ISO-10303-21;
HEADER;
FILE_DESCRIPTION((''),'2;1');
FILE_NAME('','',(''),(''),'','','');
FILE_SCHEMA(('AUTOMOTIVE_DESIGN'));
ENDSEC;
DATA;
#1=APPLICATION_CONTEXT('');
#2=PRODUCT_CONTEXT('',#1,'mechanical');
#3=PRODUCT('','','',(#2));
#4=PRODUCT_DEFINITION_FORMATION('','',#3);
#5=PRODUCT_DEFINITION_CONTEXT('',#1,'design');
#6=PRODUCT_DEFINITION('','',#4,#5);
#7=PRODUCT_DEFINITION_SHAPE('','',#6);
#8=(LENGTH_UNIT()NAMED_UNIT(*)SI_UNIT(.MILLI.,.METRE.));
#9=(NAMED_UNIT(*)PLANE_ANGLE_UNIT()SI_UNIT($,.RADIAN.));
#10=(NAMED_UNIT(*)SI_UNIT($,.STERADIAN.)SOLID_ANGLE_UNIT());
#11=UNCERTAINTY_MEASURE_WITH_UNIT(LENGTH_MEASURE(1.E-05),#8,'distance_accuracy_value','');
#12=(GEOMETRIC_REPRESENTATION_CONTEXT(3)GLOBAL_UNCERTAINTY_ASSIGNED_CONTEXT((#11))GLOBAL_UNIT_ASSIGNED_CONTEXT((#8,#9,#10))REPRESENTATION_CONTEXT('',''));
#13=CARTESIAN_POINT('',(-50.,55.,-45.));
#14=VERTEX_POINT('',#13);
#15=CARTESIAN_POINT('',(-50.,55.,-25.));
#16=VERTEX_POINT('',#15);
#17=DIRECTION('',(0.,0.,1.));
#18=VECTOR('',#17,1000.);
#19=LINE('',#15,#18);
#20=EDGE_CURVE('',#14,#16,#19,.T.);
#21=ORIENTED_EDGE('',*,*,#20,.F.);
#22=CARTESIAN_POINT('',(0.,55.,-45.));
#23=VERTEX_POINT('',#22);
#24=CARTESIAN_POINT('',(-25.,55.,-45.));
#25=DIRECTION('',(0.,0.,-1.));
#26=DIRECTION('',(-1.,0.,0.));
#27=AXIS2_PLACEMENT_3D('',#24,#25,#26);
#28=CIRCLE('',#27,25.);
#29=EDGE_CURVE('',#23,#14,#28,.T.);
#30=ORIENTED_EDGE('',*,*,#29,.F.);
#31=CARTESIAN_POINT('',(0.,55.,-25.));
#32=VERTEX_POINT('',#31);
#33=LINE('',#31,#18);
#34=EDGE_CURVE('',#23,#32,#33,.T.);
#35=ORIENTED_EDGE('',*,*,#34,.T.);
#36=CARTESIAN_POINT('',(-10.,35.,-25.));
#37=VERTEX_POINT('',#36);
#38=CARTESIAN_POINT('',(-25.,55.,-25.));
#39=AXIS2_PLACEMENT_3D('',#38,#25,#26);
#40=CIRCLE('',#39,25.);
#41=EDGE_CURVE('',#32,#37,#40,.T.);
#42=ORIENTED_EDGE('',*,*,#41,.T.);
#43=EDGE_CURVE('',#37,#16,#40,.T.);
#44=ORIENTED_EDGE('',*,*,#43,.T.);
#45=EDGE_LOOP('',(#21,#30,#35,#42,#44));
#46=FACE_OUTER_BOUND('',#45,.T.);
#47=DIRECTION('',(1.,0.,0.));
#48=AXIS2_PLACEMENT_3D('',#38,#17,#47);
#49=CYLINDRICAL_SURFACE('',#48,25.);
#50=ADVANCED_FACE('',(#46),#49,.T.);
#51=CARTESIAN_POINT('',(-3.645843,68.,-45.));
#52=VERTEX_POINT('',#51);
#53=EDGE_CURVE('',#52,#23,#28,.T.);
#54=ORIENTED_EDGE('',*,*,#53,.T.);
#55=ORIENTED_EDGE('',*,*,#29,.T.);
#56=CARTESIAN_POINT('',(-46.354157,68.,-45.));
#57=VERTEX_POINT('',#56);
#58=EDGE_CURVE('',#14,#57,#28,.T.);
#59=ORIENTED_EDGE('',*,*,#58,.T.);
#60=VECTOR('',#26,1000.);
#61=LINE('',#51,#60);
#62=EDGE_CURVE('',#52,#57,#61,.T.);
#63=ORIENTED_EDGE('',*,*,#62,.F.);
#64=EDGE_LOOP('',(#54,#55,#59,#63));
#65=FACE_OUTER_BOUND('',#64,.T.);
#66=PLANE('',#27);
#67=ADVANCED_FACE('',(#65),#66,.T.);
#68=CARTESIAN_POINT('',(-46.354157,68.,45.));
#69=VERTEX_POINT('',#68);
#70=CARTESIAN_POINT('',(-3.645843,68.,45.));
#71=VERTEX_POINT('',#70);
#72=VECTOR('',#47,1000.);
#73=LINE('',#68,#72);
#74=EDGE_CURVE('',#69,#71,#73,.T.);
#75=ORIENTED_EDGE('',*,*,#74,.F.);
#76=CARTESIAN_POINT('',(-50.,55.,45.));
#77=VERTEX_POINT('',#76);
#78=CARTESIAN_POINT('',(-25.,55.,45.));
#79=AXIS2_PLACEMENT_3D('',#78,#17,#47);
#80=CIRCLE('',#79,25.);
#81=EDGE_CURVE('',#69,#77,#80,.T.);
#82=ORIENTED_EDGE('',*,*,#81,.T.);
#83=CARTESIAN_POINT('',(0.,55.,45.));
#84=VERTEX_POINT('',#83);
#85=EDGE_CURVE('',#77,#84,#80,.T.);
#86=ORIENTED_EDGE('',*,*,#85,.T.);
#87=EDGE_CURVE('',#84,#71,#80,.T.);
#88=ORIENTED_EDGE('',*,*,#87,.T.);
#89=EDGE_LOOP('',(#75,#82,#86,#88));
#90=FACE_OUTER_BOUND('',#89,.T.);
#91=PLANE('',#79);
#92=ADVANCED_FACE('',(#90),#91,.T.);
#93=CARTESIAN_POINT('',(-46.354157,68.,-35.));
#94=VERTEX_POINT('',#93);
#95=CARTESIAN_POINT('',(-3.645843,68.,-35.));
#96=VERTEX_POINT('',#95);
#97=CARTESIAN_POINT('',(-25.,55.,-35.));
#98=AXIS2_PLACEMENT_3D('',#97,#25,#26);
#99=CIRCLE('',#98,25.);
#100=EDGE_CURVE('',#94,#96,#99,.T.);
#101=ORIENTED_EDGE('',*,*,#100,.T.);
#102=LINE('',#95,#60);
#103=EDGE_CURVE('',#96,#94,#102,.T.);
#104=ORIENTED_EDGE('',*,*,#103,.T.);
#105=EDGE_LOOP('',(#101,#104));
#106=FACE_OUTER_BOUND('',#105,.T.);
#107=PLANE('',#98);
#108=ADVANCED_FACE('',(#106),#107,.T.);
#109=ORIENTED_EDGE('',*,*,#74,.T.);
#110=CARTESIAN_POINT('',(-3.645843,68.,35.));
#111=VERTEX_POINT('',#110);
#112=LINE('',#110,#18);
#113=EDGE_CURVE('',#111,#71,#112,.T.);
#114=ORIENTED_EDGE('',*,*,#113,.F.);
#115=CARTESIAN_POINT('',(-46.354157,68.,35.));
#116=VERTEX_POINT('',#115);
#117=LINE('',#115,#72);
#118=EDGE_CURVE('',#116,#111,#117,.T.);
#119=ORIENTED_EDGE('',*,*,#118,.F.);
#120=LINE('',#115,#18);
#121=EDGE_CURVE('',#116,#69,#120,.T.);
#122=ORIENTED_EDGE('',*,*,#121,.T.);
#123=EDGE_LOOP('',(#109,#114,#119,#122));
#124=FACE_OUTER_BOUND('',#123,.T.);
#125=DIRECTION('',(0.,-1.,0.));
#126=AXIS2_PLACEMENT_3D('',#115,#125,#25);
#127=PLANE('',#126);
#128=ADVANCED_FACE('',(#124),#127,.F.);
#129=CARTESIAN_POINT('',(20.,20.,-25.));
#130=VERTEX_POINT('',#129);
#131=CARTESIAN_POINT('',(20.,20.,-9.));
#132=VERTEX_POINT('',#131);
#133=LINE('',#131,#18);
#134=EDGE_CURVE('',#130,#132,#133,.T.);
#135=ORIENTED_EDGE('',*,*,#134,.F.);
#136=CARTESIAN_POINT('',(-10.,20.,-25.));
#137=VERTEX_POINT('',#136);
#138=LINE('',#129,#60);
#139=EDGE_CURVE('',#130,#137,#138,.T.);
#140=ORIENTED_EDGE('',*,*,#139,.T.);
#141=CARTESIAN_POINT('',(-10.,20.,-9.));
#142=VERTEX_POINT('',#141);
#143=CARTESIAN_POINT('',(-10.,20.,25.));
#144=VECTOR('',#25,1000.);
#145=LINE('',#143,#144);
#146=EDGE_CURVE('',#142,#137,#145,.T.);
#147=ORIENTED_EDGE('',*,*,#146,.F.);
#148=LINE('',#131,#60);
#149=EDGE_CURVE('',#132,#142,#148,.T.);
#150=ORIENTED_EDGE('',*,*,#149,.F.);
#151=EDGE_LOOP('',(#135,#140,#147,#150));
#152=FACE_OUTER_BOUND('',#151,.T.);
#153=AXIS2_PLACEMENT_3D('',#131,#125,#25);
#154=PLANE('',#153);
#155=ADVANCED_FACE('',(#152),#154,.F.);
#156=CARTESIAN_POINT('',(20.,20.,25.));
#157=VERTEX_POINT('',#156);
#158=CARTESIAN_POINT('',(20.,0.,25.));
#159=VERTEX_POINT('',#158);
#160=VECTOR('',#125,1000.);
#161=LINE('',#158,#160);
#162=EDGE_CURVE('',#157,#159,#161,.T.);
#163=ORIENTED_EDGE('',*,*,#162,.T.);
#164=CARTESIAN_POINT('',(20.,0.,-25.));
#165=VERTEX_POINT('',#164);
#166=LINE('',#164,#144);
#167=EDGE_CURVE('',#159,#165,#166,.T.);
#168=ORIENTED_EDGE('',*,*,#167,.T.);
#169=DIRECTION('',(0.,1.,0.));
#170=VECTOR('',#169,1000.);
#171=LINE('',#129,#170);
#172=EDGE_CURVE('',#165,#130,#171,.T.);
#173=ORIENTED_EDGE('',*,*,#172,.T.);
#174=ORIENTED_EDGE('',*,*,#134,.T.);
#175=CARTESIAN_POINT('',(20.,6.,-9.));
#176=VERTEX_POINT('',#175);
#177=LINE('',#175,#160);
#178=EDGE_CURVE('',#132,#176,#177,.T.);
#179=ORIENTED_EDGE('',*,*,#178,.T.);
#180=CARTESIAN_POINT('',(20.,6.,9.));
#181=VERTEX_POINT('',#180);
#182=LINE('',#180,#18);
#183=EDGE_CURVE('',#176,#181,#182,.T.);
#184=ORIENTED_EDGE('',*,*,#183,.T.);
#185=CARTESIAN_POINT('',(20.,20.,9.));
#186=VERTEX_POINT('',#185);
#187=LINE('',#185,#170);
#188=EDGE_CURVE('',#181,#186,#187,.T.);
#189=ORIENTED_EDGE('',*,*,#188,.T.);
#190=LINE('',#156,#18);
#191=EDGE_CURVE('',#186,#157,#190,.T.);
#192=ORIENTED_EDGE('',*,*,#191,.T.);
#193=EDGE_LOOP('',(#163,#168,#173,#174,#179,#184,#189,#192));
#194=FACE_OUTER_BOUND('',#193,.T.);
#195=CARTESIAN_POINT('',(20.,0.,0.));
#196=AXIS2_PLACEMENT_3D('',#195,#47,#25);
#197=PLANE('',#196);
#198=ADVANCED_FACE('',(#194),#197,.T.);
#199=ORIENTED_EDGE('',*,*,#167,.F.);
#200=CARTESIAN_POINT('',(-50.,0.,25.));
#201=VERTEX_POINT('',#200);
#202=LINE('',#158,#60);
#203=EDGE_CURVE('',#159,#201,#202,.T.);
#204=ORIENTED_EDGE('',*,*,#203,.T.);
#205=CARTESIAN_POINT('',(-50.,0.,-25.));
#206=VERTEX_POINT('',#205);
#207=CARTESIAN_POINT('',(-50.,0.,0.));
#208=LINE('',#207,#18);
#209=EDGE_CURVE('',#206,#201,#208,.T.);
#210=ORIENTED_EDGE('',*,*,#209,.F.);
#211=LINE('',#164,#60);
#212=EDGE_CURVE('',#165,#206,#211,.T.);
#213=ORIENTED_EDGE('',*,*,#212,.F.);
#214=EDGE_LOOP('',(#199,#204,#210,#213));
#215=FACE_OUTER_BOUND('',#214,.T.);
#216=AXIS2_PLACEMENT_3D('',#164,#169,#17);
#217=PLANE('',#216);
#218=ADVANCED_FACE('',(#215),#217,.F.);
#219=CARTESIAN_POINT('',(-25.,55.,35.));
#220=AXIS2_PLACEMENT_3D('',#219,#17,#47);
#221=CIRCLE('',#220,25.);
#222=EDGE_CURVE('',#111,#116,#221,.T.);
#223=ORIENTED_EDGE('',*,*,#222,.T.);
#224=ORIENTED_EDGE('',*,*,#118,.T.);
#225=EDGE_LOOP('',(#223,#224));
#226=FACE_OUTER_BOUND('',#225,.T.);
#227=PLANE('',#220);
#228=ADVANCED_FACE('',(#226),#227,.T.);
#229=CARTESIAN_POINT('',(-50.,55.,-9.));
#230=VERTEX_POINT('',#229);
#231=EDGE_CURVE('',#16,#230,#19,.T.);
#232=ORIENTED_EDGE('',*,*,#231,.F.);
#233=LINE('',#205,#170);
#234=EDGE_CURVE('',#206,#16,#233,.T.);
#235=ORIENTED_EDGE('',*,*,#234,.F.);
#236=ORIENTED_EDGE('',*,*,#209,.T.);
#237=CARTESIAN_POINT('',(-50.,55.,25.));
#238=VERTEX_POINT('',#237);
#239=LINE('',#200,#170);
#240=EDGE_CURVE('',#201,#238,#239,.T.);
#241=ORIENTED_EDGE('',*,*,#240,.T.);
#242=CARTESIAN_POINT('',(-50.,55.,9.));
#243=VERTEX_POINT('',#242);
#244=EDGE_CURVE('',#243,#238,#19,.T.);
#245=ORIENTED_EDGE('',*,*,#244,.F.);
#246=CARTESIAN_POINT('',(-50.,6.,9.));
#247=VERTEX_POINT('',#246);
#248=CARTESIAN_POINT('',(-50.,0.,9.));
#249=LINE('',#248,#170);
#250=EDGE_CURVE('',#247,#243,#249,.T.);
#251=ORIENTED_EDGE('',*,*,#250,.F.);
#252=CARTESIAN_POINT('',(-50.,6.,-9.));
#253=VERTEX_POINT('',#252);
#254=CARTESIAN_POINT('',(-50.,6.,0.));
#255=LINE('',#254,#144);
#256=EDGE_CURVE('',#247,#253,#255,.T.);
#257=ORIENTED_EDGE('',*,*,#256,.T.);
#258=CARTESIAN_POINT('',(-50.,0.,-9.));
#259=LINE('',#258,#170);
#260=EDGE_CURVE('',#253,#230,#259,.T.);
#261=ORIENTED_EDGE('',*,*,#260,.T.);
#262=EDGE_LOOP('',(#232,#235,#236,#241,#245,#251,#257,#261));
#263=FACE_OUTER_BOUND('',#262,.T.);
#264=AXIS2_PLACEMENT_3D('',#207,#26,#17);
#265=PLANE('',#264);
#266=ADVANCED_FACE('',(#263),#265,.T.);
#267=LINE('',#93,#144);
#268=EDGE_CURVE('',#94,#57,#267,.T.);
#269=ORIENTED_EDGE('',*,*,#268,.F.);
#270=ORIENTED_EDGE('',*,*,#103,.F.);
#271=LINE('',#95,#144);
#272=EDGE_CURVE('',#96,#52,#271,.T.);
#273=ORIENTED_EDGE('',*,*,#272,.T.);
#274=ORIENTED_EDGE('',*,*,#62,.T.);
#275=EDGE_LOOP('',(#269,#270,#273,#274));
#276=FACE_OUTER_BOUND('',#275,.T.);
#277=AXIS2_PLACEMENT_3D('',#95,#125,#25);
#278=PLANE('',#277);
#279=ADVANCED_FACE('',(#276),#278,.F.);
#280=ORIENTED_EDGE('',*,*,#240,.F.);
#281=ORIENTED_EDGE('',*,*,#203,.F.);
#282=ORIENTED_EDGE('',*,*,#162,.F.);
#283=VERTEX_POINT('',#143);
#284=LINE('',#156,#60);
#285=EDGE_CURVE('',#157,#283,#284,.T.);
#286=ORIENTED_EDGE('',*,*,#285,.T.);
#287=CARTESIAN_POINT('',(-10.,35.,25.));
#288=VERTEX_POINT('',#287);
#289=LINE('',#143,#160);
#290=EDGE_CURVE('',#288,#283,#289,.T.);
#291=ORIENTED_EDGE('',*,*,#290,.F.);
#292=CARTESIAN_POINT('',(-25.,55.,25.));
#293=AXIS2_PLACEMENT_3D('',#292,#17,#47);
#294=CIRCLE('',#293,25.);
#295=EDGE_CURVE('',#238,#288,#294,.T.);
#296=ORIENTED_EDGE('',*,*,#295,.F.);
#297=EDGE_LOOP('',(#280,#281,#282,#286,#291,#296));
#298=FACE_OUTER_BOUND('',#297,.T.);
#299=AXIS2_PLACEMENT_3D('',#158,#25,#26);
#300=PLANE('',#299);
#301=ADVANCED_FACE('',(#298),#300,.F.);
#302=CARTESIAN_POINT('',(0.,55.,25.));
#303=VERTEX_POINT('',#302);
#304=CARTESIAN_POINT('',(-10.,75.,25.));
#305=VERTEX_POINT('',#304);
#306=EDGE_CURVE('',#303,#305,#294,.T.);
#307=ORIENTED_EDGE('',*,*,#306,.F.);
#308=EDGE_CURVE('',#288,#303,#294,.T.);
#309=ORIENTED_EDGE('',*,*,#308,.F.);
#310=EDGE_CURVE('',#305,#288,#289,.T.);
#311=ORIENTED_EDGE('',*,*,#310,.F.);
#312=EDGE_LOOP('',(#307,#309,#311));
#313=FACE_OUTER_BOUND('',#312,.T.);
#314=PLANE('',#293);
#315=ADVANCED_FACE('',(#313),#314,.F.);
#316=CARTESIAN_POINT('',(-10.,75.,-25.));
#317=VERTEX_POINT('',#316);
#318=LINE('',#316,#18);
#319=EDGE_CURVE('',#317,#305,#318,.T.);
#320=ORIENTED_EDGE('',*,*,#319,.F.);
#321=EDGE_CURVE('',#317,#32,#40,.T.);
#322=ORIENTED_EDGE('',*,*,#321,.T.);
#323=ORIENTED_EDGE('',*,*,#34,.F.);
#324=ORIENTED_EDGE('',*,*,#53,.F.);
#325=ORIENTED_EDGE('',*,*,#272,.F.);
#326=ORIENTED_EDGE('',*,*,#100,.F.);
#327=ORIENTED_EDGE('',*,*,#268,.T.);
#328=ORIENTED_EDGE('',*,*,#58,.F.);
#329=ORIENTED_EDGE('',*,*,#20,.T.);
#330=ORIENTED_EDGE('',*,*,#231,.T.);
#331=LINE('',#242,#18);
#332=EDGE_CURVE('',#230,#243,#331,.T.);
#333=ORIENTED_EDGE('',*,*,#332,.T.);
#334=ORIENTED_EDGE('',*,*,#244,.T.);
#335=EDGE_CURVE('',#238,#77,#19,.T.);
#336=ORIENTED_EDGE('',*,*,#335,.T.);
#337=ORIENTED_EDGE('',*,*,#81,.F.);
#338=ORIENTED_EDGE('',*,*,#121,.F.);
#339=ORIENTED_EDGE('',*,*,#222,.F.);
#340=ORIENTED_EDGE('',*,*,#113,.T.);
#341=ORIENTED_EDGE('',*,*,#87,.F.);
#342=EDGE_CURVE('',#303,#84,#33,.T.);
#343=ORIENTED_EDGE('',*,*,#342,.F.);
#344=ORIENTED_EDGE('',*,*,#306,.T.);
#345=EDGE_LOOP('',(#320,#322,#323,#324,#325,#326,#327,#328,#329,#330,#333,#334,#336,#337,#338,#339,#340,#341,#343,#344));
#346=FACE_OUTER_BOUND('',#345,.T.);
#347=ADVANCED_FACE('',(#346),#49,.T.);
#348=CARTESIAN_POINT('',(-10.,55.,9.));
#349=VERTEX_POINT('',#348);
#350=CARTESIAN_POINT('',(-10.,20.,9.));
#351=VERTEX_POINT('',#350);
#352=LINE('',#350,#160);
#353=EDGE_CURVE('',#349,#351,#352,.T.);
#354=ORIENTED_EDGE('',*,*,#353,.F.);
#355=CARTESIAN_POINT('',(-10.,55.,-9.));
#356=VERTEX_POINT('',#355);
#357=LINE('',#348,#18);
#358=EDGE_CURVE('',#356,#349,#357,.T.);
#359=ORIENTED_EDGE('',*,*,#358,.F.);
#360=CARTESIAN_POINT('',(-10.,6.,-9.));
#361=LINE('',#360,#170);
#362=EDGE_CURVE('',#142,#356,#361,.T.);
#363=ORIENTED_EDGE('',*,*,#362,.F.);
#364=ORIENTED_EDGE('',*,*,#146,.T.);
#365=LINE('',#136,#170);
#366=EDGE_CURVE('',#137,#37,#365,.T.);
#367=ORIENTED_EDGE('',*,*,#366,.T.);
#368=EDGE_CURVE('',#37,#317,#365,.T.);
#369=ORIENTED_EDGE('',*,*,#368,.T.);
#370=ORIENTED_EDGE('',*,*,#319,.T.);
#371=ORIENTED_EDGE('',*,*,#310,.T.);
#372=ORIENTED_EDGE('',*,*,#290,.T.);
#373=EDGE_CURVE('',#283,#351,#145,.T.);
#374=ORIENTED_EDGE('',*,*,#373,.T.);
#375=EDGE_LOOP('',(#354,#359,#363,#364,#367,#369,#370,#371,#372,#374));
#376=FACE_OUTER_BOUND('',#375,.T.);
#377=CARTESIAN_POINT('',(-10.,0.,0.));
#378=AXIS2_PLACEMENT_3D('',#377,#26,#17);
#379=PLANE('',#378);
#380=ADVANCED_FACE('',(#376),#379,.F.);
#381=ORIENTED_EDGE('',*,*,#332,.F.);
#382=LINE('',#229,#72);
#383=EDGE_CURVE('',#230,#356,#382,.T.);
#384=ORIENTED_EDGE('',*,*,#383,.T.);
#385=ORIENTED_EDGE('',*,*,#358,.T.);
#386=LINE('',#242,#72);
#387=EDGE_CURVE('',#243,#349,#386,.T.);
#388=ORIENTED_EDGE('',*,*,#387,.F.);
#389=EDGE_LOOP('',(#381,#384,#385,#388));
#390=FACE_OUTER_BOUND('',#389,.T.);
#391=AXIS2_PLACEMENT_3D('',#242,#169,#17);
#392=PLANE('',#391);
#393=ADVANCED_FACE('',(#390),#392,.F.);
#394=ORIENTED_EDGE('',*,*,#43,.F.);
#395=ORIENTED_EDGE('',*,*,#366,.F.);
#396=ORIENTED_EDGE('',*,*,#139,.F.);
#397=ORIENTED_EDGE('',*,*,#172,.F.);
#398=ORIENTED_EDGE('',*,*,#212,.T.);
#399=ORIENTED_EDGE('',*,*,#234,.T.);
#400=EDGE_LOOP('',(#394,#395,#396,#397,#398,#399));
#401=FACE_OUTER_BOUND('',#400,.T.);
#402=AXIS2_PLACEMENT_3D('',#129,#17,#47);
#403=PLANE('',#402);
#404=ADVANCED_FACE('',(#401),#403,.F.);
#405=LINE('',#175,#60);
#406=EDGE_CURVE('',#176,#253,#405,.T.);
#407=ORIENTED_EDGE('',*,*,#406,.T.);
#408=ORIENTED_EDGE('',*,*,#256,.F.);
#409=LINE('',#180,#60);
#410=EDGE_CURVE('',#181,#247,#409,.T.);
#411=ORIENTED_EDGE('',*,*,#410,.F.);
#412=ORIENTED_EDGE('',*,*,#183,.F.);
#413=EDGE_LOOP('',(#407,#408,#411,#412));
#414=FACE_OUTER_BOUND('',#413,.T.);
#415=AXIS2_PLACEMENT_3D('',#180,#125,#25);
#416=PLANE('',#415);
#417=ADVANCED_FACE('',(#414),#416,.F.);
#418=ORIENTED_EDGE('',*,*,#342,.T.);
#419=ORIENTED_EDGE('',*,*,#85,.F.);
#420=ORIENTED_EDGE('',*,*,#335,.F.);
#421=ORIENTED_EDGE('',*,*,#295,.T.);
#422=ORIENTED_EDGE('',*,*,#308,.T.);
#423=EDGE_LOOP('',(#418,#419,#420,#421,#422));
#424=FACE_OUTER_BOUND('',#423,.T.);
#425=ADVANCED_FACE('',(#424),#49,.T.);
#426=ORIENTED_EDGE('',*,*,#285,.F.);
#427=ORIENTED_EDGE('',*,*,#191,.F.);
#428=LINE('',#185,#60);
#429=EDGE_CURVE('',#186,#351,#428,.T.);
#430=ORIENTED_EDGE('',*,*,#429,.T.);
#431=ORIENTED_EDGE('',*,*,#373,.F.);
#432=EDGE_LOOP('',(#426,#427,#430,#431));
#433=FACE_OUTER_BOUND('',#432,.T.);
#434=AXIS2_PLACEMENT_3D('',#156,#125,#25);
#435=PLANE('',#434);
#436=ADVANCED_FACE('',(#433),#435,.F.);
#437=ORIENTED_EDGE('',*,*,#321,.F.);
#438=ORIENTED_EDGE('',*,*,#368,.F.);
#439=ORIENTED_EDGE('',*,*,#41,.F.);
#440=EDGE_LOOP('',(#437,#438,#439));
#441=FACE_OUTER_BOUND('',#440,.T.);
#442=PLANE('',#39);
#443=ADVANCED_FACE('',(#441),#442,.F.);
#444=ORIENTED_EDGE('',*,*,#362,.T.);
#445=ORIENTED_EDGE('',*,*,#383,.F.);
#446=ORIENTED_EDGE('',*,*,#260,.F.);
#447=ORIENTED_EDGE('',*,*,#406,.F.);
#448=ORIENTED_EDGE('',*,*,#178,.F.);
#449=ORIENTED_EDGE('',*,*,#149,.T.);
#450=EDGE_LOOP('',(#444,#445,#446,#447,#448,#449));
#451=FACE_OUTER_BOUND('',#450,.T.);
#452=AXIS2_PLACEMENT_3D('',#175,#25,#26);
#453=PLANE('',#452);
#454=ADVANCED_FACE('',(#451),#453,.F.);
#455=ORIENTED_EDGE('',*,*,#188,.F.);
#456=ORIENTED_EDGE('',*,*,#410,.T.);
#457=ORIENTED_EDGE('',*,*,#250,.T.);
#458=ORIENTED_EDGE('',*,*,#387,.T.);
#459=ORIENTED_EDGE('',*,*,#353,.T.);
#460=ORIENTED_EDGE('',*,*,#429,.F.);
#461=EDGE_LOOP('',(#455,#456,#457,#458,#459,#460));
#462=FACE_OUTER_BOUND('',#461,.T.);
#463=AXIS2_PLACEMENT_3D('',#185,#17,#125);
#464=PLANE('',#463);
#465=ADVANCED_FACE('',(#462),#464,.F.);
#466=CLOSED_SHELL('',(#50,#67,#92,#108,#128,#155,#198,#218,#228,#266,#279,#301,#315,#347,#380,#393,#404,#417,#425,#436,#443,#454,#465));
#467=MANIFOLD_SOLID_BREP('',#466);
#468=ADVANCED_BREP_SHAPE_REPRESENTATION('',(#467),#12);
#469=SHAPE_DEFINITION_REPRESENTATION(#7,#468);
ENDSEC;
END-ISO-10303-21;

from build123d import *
from build123d.topology import SkipClean

# Parameters (mm, degrees)
U_BASE_DEPTH             = 20
UPRIGHT_WEB_DEPTH        = 50
CYLINDER_50_SKETCH_R     = 25
CYLINDER_50_DEPTH        = 50
WEB_CLEARANCE_CUT_DEPTH  = 50
SIDE_RELIEF_CUT_SKETCH_W = 18
SIDE_RELIEF_CUT_SKETCH_H = 35
SIDE_RELIEF_CUT_DEPTH    = 50
BASE_SLOT_CUT_SKETCH_W   = 50
BASE_SLOT_CUT_SKETCH_H   = 50
BASE_SLOT_CUT_DEPTH      = 10
WEB_SLOT_CUT_SKETCH_W    = 5
WEB_SLOT_CUT_SKETCH_H    = 50
WEB_SLOT_CUT_DEPTH       = 10
END_START                = 20
END_BOSS_A_SKETCH_R      = 25
END_BOSS_A_50_DEPTH      = 20
END_BOSS_B_SKETCH_R      = 25
END_BOSS_B_50_DEPTH      = 20
END_SLOT_A_DEPTH         = 10
END_START_2              = -10
END_SLOT_B_DEPTH         = 10


with BuildPart() as part:
    # U Base Profile Sketch → U Base (new body)
    with BuildSketch(Plane(origin=(0, 0, 0), x_dir=(0, 0, -1), z_dir=(1, 0, 0))):
        Polygon((25, 0), (-25, 0), (-25, 20), (-9, 20), (-9, 6), (9, 6), (9, 20), (25, 20), align=None)
    extrude(amount=U_BASE_DEPTH)

    # Upright Web Sketch → Upright Web (add)
    with BuildSketch(Plane.ZY):
        Polygon((-9, 20), (-9, 65), (9, 65), (9, 20), (25, 20), (25, 70), (-25, 70), (-25, 20), align=None)
        Polygon((25, 20), (9, 20), (9, 6), (-9, 6), (-9, 20), (-25, 20), (-25, 0), (25, 0), align=None)
    extrude(amount=UPRIGHT_WEB_DEPTH)

    # Cylinder Ø50 Sketch → Cylinder Ø50 (add)
    with BuildSketch(Plane.XY.offset(25)):
        with Locations((-25, 55)):
            Circle(CYLINDER_50_SKETCH_R)
    extrude(amount=-CYLINDER_50_DEPTH)

    # Web Clearance Cut Sketch → Web Clearance Cut (cut)
    with SkipClean():  # the faces are left unmerged after this step: merging them gives an invalid solid
        with BuildSketch(Plane.XY.offset(25)):
            with BuildLine():
                Line((-50, 70), (-50, 55))
                ThreePointArc((-50, 55), (-48.717082, 62.905694), (-45, 70))
                Line((-45, 70), (-50, 70))
            make_face()
            with BuildLine():
                ThreePointArc((-5, 70), (-1.282918, 62.905694), (0, 55))
                Line((0, 55), (0, 70))
                Line((0, 70), (-5, 70))
            make_face()
        extrude(amount=-WEB_CLEARANCE_CUT_DEPTH, mode=Mode.SUBTRACT)

    # Side Relief Cut Sketch → Side Relief Cut (cut)
    with SkipClean():  # the faces are left unmerged after this step: merging them gives an invalid solid
        with BuildSketch(Plane(origin=(0, 0, 0), x_dir=(0, 0, -1), z_dir=(1, 0, 0))):
            with Locations((0, 37.5)):
                Rectangle(SIDE_RELIEF_CUT_SKETCH_W, SIDE_RELIEF_CUT_SKETCH_H)
        extrude(amount=-SIDE_RELIEF_CUT_DEPTH, mode=Mode.SUBTRACT)

    # Base Slot Cut Sketch → Base Slot Cut (cut)
    with SkipClean():  # the faces are left unmerged after this step: merging them gives an invalid solid
        with BuildSketch(Plane(origin=(0, 0, 0), x_dir=(0, 0, -1), z_dir=(1, 0, 0))):
            with Locations((0, 45)):
                Rectangle(BASE_SLOT_CUT_SKETCH_W, BASE_SLOT_CUT_SKETCH_H)
        extrude(amount=-BASE_SLOT_CUT_DEPTH, mode=Mode.SUBTRACT)

    # Web Slot Cut Sketch → Web Slot Cut (cut)
    with SkipClean():  # the faces are left unmerged after this step: merging them gives an invalid solid
        with BuildSketch(Plane.XZ.offset(-70)):
            with Locations((-7.5, 0)):
                Rectangle(WEB_SLOT_CUT_SKETCH_W, WEB_SLOT_CUT_SKETCH_H)
        extrude(amount=-WEB_SLOT_CUT_DEPTH, mode=Mode.SUBTRACT)

    # End Boss A Sketch → End Boss A Ø50 (add)
    with BuildSketch(Plane.XY.offset(25).offset(END_START)):
        with Locations((-25, 55)):
            Circle(END_BOSS_A_SKETCH_R)
    extrude(amount=-END_BOSS_A_50_DEPTH)

    # End Boss B Sketch → End Boss B Ø50 (add)
    with BuildSketch(Plane(origin=(0, 0, -25), x_dir=(-1, 0, 0), z_dir=(0, 0, -1))):
        with Locations(Location((25, 55, 0), (0, 0, 180))):
            Circle(END_BOSS_B_SKETCH_R)
    extrude(amount=END_BOSS_B_50_DEPTH)

    # End Slot A Sketch → End Slot A (cut)
    with BuildSketch(Plane.XY.offset(45)):
        with BuildLine():
            Line((-46.354157, 68), (-3.645843, 68))
            ThreePointArc((-3.645843, 68), (-25, 80), (-46.354157, 68))
        make_face()
    extrude(amount=-END_SLOT_A_DEPTH, mode=Mode.SUBTRACT)

    # End Slot B Sketch → End Slot B (cut)
    with BuildSketch(Plane(origin=(0, 0, -45), x_dir=(-1, 0, 0), z_dir=(0, 0, -1)).offset(END_START_2)):
        with BuildLine():
            Line((3.645843, 68), (46.354157, 68))
            ThreePointArc((46.354157, 68), (25, 80), (3.645843, 68))
        make_face()
    extrude(amount=END_SLOT_B_DEPTH, mode=Mode.SUBTRACT)


solid = part.part
